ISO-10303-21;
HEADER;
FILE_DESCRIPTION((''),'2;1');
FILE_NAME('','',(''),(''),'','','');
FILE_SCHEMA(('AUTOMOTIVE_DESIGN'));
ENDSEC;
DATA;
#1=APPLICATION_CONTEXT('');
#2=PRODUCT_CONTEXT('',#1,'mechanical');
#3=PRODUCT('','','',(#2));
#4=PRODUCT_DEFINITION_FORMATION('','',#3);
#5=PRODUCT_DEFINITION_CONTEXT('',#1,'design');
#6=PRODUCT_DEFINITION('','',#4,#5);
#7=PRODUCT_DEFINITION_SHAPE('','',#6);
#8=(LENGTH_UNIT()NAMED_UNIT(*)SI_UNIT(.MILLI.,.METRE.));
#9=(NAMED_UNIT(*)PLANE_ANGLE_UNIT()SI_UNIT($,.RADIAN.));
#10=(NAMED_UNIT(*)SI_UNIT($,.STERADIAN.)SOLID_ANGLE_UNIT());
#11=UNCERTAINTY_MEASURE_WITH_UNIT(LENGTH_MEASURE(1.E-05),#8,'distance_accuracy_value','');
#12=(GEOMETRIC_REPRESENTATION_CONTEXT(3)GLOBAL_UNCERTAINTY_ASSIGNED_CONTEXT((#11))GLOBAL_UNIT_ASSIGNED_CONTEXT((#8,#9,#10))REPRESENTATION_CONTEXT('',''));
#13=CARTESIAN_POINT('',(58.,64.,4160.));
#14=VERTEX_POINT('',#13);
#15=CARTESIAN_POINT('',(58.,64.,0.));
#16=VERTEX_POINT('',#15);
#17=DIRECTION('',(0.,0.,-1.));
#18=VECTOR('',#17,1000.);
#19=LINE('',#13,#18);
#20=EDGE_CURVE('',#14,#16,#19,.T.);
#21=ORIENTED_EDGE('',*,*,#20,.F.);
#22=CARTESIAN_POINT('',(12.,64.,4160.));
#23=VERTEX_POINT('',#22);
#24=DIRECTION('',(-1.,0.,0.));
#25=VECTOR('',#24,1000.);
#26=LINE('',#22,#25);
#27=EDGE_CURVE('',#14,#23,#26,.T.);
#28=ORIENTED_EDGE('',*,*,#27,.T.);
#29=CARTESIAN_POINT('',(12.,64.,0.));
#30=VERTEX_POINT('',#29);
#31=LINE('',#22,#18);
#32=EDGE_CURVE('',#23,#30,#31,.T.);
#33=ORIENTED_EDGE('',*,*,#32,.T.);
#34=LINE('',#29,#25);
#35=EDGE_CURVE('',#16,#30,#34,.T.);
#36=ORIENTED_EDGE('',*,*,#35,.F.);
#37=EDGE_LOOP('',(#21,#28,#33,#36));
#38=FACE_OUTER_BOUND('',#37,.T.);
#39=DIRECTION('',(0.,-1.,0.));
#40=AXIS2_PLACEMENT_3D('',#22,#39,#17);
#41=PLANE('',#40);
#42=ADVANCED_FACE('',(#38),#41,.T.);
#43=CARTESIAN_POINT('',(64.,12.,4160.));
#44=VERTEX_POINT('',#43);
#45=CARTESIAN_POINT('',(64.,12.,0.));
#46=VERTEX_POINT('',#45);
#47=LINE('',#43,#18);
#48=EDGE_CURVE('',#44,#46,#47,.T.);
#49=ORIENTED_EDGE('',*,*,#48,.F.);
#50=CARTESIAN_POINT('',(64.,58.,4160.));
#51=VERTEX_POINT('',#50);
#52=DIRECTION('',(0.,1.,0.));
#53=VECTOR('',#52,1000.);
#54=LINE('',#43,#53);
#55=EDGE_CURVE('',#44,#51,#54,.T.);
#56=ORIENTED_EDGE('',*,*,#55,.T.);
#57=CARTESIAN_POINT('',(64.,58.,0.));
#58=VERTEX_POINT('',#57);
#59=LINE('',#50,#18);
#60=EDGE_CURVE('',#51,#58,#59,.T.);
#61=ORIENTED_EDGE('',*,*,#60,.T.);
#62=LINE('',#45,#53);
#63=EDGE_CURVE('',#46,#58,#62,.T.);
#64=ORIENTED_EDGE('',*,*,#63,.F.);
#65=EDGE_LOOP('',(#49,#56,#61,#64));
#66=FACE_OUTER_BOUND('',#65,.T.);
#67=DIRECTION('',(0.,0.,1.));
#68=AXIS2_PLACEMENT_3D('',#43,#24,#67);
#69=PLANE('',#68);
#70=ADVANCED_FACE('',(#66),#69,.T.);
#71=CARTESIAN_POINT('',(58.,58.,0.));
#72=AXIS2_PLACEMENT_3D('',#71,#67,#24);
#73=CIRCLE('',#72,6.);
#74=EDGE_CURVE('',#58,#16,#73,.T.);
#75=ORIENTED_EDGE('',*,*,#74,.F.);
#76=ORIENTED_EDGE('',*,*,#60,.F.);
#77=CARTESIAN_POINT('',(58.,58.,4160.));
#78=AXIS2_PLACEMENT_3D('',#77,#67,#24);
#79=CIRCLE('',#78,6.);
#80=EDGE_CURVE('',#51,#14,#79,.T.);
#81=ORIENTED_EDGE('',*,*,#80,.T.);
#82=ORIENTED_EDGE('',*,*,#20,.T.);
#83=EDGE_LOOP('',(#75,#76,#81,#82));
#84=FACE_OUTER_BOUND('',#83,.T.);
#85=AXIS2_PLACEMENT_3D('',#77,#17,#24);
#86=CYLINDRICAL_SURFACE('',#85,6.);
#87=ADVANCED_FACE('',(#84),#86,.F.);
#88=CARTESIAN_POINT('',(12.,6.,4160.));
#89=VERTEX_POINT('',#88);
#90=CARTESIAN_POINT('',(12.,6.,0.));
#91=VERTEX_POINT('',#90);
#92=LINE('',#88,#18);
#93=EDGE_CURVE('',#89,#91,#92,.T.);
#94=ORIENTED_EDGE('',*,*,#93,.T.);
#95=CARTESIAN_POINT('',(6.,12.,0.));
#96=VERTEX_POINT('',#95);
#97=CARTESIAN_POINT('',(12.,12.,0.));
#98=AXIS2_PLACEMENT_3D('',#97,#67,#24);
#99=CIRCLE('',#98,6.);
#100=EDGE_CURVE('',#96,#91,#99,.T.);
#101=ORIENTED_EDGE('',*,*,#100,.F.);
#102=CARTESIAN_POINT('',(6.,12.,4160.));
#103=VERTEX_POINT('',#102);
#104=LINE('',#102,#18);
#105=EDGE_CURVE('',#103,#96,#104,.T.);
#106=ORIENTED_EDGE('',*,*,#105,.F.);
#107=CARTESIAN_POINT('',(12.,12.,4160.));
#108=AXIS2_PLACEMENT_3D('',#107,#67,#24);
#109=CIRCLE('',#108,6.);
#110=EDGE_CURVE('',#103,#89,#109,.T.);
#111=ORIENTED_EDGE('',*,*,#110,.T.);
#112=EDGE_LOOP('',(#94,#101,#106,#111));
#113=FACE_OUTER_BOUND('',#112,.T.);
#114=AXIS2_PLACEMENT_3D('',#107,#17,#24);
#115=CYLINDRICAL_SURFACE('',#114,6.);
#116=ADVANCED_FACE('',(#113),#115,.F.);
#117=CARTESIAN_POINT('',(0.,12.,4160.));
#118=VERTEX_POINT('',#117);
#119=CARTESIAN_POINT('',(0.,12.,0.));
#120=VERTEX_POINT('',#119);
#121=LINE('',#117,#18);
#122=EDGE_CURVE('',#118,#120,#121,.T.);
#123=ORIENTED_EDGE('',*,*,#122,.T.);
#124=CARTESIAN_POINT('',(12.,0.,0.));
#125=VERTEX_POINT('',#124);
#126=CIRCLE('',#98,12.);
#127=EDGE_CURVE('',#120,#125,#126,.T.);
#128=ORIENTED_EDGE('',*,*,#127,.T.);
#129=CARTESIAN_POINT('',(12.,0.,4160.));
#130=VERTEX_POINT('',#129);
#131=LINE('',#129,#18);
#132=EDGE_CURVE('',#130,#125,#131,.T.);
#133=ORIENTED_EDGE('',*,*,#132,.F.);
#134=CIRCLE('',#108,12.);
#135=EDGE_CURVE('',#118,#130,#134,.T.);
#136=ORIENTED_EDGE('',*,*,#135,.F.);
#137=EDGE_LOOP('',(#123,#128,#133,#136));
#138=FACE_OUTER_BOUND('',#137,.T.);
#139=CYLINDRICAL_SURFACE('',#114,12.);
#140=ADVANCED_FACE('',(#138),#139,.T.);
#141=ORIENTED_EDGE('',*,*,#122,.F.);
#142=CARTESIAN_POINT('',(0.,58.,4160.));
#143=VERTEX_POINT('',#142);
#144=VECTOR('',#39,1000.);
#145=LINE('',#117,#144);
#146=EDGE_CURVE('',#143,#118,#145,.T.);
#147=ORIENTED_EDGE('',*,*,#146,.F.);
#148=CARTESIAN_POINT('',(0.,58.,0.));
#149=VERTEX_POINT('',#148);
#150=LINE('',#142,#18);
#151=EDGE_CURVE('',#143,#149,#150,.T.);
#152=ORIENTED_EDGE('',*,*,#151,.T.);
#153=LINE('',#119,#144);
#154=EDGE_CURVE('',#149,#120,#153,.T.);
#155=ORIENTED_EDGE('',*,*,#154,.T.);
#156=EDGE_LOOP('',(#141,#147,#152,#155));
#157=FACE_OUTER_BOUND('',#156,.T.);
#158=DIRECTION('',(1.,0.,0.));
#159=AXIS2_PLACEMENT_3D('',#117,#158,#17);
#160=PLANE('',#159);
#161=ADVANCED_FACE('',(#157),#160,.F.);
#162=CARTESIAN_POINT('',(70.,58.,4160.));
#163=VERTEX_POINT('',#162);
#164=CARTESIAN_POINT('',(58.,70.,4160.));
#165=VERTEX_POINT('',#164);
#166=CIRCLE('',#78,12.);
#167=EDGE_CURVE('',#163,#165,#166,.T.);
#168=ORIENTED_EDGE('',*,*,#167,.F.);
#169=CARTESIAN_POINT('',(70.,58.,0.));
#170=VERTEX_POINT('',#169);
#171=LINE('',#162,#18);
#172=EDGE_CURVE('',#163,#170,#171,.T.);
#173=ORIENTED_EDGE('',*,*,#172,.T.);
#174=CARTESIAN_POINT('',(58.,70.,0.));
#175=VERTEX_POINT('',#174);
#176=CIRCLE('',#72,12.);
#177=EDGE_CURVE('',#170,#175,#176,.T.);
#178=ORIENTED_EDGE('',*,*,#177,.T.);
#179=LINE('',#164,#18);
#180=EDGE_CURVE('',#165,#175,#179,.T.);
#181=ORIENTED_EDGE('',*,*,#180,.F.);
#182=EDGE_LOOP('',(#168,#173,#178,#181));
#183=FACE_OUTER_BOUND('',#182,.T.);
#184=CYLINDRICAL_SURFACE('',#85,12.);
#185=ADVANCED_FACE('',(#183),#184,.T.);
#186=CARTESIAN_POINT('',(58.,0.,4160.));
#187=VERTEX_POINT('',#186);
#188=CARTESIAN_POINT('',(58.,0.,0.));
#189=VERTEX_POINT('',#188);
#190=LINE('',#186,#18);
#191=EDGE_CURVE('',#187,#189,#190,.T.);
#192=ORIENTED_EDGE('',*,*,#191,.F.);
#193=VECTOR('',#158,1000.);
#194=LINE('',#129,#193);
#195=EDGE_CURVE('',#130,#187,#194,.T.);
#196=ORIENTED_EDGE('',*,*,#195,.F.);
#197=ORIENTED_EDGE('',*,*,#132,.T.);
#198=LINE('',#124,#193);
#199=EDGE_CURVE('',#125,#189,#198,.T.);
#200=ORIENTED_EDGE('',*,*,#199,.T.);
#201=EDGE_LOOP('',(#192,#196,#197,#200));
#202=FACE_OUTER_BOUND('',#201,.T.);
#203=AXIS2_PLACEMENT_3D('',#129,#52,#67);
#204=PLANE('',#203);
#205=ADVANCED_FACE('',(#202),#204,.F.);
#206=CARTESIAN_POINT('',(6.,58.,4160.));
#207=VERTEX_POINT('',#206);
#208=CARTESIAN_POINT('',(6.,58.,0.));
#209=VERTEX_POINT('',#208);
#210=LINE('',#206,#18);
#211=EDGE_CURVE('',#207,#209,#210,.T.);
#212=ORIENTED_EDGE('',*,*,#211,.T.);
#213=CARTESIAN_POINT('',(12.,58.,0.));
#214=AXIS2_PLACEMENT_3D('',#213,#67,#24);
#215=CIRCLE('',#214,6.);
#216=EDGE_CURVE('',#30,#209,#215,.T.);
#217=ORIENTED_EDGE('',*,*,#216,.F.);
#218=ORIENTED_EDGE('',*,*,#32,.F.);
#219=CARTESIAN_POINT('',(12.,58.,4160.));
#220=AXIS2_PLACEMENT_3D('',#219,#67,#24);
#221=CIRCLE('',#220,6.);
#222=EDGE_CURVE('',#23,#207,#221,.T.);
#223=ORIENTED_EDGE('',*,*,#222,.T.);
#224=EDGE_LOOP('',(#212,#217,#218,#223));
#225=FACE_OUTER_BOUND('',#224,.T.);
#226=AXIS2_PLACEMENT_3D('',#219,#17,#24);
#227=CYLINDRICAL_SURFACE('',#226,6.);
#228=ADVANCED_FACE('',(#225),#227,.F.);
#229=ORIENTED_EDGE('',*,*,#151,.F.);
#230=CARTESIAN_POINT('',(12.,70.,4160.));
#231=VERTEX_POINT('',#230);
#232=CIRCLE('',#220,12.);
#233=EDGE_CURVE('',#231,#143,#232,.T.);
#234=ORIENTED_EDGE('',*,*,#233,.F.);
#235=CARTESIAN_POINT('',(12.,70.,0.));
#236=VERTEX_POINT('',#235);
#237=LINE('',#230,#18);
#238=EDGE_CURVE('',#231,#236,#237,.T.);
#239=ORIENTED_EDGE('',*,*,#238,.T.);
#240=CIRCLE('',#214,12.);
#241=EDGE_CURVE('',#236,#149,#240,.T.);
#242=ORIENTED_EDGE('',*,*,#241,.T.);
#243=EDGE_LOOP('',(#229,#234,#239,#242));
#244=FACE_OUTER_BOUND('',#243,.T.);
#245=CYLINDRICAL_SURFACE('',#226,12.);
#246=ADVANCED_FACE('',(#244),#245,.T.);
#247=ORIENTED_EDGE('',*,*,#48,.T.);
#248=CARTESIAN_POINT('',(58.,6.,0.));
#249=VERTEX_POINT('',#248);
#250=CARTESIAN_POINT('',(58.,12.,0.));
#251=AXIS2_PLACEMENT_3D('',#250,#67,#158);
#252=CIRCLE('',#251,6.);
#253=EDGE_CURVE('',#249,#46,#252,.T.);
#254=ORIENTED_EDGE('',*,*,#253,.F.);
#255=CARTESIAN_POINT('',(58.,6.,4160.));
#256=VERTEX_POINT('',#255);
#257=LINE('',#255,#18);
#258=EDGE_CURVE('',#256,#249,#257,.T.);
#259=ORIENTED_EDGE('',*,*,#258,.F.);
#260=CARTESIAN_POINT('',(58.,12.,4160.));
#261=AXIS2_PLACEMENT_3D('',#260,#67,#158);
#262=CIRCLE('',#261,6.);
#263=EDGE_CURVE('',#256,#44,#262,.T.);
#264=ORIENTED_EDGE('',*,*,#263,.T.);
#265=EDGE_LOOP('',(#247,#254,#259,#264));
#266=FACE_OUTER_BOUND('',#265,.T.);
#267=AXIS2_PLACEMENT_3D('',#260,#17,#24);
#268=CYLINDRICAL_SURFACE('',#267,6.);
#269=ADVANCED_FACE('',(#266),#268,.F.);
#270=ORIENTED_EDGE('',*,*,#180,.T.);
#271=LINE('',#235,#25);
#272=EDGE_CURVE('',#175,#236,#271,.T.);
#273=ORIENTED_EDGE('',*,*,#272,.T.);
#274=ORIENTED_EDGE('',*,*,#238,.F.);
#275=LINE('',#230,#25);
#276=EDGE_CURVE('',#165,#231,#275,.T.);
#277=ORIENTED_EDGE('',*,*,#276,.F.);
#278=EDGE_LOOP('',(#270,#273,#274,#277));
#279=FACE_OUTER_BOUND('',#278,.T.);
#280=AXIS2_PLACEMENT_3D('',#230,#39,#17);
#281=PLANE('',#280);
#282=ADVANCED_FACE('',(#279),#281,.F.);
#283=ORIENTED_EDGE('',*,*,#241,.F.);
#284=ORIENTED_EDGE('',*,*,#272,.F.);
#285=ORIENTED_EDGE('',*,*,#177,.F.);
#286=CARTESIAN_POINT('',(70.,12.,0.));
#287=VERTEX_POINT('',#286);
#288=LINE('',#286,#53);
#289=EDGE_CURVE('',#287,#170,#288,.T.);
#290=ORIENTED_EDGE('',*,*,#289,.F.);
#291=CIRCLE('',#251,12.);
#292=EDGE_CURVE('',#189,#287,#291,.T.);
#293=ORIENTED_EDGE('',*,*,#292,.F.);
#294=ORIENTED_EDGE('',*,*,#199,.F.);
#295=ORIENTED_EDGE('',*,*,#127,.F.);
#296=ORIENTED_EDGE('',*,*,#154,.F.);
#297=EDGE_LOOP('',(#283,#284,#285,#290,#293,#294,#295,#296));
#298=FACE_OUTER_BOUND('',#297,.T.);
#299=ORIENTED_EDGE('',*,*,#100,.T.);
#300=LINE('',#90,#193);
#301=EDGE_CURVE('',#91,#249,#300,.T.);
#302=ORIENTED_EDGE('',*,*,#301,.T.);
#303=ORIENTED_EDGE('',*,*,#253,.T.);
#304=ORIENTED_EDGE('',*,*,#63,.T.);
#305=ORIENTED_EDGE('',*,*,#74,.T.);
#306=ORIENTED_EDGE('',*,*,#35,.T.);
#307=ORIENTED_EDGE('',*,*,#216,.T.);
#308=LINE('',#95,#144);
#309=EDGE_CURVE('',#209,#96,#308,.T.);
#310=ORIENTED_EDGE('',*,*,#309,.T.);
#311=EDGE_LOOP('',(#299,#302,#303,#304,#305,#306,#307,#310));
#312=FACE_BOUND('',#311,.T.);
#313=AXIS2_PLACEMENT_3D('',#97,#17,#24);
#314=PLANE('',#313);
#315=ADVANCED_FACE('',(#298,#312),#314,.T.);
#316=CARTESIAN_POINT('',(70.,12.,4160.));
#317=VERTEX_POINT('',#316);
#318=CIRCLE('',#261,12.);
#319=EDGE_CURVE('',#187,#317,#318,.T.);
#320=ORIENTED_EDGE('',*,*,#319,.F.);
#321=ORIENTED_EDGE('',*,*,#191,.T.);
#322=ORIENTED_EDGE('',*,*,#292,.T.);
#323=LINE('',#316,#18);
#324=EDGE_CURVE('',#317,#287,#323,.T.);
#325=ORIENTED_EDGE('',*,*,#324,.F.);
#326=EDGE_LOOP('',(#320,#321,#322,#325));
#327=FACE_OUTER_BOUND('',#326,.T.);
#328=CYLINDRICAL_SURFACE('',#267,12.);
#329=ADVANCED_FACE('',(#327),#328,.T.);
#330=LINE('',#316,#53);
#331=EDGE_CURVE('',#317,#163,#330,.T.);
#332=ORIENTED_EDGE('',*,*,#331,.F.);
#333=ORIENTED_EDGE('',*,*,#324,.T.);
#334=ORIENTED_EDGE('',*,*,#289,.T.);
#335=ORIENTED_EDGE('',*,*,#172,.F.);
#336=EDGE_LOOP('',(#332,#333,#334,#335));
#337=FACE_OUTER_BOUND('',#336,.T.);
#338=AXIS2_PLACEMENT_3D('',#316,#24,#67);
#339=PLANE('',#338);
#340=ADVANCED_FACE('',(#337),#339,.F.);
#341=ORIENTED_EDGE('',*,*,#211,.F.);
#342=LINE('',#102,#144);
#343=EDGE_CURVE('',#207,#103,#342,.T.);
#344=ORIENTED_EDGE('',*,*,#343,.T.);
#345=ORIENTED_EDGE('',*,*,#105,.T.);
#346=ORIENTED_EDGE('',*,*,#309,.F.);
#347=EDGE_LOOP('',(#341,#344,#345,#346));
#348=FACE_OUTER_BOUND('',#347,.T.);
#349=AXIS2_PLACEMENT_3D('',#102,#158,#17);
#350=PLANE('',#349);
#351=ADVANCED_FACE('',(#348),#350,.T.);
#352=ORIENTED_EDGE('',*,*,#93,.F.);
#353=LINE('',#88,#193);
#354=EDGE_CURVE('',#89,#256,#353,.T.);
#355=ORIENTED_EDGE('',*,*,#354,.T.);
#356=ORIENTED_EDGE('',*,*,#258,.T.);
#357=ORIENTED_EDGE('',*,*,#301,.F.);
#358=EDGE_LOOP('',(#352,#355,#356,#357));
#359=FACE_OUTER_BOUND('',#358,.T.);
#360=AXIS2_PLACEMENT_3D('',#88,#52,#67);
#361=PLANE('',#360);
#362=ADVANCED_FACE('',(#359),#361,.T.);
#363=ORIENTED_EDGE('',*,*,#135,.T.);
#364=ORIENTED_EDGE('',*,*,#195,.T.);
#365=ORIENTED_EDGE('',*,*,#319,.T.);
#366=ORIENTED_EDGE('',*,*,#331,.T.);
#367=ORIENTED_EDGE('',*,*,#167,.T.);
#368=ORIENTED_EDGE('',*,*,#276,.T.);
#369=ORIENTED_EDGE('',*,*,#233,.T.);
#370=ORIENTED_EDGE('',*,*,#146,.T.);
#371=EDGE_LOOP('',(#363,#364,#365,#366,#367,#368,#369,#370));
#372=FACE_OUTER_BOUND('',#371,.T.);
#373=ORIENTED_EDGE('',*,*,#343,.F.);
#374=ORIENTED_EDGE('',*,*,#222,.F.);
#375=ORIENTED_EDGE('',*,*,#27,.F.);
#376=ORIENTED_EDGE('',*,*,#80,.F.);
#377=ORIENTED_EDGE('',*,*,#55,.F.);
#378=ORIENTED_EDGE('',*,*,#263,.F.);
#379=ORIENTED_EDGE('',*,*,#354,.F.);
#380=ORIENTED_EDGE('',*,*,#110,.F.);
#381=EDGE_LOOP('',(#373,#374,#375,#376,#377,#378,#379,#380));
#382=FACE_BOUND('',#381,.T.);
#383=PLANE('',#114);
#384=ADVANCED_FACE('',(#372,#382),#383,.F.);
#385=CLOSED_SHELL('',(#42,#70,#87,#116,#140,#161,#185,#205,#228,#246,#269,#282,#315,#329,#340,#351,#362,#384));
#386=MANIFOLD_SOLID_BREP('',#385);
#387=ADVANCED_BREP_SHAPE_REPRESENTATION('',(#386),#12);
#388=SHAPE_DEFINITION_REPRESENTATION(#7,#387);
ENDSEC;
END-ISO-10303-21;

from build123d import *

# Parameters (mm, degrees)
BOSS_EXTRUDE1_DEPTH = 4160


with BuildPart() as part:
    # Sketch1 → Boss-Extrude1 (new body)
    with BuildSketch(Plane.XY):
        with BuildLine():
            Line((12, 0), (58, 0))
            ThreePointArc((58, 0), (66.485281374, 3.514718626), (70, 12))
            Line((70, 12), (70, 58))
            ThreePointArc((70, 58), (66.485281374, 66.485281374), (58, 70))
            Line((58, 70), (12, 70))
            ThreePointArc((12, 70), (3.514718626, 66.485281374), (0, 58))
            Line((0, 58), (0, 12))
            ThreePointArc((0, 12), (3.514718626, 3.514718626), (12, 0))
        make_face()
        with BuildLine():
            Line((12, 6), (58, 6))
            ThreePointArc((58, 6), (62.242640687, 7.757359313), (64, 12))
            Line((64, 12), (64, 58))
            ThreePointArc((64, 58), (62.242640687, 62.242640687), (58, 64))
            Line((58, 64), (12, 64))
            ThreePointArc((12, 64), (7.757359313, 62.242640687), (6, 58))
            Line((6, 58), (6, 12))
            ThreePointArc((6, 12), (7.757359313, 7.757359313), (12, 6))
        make_face(mode=Mode.SUBTRACT)
    extrude(amount=BOSS_EXTRUDE1_DEPTH)


solid = part.part
